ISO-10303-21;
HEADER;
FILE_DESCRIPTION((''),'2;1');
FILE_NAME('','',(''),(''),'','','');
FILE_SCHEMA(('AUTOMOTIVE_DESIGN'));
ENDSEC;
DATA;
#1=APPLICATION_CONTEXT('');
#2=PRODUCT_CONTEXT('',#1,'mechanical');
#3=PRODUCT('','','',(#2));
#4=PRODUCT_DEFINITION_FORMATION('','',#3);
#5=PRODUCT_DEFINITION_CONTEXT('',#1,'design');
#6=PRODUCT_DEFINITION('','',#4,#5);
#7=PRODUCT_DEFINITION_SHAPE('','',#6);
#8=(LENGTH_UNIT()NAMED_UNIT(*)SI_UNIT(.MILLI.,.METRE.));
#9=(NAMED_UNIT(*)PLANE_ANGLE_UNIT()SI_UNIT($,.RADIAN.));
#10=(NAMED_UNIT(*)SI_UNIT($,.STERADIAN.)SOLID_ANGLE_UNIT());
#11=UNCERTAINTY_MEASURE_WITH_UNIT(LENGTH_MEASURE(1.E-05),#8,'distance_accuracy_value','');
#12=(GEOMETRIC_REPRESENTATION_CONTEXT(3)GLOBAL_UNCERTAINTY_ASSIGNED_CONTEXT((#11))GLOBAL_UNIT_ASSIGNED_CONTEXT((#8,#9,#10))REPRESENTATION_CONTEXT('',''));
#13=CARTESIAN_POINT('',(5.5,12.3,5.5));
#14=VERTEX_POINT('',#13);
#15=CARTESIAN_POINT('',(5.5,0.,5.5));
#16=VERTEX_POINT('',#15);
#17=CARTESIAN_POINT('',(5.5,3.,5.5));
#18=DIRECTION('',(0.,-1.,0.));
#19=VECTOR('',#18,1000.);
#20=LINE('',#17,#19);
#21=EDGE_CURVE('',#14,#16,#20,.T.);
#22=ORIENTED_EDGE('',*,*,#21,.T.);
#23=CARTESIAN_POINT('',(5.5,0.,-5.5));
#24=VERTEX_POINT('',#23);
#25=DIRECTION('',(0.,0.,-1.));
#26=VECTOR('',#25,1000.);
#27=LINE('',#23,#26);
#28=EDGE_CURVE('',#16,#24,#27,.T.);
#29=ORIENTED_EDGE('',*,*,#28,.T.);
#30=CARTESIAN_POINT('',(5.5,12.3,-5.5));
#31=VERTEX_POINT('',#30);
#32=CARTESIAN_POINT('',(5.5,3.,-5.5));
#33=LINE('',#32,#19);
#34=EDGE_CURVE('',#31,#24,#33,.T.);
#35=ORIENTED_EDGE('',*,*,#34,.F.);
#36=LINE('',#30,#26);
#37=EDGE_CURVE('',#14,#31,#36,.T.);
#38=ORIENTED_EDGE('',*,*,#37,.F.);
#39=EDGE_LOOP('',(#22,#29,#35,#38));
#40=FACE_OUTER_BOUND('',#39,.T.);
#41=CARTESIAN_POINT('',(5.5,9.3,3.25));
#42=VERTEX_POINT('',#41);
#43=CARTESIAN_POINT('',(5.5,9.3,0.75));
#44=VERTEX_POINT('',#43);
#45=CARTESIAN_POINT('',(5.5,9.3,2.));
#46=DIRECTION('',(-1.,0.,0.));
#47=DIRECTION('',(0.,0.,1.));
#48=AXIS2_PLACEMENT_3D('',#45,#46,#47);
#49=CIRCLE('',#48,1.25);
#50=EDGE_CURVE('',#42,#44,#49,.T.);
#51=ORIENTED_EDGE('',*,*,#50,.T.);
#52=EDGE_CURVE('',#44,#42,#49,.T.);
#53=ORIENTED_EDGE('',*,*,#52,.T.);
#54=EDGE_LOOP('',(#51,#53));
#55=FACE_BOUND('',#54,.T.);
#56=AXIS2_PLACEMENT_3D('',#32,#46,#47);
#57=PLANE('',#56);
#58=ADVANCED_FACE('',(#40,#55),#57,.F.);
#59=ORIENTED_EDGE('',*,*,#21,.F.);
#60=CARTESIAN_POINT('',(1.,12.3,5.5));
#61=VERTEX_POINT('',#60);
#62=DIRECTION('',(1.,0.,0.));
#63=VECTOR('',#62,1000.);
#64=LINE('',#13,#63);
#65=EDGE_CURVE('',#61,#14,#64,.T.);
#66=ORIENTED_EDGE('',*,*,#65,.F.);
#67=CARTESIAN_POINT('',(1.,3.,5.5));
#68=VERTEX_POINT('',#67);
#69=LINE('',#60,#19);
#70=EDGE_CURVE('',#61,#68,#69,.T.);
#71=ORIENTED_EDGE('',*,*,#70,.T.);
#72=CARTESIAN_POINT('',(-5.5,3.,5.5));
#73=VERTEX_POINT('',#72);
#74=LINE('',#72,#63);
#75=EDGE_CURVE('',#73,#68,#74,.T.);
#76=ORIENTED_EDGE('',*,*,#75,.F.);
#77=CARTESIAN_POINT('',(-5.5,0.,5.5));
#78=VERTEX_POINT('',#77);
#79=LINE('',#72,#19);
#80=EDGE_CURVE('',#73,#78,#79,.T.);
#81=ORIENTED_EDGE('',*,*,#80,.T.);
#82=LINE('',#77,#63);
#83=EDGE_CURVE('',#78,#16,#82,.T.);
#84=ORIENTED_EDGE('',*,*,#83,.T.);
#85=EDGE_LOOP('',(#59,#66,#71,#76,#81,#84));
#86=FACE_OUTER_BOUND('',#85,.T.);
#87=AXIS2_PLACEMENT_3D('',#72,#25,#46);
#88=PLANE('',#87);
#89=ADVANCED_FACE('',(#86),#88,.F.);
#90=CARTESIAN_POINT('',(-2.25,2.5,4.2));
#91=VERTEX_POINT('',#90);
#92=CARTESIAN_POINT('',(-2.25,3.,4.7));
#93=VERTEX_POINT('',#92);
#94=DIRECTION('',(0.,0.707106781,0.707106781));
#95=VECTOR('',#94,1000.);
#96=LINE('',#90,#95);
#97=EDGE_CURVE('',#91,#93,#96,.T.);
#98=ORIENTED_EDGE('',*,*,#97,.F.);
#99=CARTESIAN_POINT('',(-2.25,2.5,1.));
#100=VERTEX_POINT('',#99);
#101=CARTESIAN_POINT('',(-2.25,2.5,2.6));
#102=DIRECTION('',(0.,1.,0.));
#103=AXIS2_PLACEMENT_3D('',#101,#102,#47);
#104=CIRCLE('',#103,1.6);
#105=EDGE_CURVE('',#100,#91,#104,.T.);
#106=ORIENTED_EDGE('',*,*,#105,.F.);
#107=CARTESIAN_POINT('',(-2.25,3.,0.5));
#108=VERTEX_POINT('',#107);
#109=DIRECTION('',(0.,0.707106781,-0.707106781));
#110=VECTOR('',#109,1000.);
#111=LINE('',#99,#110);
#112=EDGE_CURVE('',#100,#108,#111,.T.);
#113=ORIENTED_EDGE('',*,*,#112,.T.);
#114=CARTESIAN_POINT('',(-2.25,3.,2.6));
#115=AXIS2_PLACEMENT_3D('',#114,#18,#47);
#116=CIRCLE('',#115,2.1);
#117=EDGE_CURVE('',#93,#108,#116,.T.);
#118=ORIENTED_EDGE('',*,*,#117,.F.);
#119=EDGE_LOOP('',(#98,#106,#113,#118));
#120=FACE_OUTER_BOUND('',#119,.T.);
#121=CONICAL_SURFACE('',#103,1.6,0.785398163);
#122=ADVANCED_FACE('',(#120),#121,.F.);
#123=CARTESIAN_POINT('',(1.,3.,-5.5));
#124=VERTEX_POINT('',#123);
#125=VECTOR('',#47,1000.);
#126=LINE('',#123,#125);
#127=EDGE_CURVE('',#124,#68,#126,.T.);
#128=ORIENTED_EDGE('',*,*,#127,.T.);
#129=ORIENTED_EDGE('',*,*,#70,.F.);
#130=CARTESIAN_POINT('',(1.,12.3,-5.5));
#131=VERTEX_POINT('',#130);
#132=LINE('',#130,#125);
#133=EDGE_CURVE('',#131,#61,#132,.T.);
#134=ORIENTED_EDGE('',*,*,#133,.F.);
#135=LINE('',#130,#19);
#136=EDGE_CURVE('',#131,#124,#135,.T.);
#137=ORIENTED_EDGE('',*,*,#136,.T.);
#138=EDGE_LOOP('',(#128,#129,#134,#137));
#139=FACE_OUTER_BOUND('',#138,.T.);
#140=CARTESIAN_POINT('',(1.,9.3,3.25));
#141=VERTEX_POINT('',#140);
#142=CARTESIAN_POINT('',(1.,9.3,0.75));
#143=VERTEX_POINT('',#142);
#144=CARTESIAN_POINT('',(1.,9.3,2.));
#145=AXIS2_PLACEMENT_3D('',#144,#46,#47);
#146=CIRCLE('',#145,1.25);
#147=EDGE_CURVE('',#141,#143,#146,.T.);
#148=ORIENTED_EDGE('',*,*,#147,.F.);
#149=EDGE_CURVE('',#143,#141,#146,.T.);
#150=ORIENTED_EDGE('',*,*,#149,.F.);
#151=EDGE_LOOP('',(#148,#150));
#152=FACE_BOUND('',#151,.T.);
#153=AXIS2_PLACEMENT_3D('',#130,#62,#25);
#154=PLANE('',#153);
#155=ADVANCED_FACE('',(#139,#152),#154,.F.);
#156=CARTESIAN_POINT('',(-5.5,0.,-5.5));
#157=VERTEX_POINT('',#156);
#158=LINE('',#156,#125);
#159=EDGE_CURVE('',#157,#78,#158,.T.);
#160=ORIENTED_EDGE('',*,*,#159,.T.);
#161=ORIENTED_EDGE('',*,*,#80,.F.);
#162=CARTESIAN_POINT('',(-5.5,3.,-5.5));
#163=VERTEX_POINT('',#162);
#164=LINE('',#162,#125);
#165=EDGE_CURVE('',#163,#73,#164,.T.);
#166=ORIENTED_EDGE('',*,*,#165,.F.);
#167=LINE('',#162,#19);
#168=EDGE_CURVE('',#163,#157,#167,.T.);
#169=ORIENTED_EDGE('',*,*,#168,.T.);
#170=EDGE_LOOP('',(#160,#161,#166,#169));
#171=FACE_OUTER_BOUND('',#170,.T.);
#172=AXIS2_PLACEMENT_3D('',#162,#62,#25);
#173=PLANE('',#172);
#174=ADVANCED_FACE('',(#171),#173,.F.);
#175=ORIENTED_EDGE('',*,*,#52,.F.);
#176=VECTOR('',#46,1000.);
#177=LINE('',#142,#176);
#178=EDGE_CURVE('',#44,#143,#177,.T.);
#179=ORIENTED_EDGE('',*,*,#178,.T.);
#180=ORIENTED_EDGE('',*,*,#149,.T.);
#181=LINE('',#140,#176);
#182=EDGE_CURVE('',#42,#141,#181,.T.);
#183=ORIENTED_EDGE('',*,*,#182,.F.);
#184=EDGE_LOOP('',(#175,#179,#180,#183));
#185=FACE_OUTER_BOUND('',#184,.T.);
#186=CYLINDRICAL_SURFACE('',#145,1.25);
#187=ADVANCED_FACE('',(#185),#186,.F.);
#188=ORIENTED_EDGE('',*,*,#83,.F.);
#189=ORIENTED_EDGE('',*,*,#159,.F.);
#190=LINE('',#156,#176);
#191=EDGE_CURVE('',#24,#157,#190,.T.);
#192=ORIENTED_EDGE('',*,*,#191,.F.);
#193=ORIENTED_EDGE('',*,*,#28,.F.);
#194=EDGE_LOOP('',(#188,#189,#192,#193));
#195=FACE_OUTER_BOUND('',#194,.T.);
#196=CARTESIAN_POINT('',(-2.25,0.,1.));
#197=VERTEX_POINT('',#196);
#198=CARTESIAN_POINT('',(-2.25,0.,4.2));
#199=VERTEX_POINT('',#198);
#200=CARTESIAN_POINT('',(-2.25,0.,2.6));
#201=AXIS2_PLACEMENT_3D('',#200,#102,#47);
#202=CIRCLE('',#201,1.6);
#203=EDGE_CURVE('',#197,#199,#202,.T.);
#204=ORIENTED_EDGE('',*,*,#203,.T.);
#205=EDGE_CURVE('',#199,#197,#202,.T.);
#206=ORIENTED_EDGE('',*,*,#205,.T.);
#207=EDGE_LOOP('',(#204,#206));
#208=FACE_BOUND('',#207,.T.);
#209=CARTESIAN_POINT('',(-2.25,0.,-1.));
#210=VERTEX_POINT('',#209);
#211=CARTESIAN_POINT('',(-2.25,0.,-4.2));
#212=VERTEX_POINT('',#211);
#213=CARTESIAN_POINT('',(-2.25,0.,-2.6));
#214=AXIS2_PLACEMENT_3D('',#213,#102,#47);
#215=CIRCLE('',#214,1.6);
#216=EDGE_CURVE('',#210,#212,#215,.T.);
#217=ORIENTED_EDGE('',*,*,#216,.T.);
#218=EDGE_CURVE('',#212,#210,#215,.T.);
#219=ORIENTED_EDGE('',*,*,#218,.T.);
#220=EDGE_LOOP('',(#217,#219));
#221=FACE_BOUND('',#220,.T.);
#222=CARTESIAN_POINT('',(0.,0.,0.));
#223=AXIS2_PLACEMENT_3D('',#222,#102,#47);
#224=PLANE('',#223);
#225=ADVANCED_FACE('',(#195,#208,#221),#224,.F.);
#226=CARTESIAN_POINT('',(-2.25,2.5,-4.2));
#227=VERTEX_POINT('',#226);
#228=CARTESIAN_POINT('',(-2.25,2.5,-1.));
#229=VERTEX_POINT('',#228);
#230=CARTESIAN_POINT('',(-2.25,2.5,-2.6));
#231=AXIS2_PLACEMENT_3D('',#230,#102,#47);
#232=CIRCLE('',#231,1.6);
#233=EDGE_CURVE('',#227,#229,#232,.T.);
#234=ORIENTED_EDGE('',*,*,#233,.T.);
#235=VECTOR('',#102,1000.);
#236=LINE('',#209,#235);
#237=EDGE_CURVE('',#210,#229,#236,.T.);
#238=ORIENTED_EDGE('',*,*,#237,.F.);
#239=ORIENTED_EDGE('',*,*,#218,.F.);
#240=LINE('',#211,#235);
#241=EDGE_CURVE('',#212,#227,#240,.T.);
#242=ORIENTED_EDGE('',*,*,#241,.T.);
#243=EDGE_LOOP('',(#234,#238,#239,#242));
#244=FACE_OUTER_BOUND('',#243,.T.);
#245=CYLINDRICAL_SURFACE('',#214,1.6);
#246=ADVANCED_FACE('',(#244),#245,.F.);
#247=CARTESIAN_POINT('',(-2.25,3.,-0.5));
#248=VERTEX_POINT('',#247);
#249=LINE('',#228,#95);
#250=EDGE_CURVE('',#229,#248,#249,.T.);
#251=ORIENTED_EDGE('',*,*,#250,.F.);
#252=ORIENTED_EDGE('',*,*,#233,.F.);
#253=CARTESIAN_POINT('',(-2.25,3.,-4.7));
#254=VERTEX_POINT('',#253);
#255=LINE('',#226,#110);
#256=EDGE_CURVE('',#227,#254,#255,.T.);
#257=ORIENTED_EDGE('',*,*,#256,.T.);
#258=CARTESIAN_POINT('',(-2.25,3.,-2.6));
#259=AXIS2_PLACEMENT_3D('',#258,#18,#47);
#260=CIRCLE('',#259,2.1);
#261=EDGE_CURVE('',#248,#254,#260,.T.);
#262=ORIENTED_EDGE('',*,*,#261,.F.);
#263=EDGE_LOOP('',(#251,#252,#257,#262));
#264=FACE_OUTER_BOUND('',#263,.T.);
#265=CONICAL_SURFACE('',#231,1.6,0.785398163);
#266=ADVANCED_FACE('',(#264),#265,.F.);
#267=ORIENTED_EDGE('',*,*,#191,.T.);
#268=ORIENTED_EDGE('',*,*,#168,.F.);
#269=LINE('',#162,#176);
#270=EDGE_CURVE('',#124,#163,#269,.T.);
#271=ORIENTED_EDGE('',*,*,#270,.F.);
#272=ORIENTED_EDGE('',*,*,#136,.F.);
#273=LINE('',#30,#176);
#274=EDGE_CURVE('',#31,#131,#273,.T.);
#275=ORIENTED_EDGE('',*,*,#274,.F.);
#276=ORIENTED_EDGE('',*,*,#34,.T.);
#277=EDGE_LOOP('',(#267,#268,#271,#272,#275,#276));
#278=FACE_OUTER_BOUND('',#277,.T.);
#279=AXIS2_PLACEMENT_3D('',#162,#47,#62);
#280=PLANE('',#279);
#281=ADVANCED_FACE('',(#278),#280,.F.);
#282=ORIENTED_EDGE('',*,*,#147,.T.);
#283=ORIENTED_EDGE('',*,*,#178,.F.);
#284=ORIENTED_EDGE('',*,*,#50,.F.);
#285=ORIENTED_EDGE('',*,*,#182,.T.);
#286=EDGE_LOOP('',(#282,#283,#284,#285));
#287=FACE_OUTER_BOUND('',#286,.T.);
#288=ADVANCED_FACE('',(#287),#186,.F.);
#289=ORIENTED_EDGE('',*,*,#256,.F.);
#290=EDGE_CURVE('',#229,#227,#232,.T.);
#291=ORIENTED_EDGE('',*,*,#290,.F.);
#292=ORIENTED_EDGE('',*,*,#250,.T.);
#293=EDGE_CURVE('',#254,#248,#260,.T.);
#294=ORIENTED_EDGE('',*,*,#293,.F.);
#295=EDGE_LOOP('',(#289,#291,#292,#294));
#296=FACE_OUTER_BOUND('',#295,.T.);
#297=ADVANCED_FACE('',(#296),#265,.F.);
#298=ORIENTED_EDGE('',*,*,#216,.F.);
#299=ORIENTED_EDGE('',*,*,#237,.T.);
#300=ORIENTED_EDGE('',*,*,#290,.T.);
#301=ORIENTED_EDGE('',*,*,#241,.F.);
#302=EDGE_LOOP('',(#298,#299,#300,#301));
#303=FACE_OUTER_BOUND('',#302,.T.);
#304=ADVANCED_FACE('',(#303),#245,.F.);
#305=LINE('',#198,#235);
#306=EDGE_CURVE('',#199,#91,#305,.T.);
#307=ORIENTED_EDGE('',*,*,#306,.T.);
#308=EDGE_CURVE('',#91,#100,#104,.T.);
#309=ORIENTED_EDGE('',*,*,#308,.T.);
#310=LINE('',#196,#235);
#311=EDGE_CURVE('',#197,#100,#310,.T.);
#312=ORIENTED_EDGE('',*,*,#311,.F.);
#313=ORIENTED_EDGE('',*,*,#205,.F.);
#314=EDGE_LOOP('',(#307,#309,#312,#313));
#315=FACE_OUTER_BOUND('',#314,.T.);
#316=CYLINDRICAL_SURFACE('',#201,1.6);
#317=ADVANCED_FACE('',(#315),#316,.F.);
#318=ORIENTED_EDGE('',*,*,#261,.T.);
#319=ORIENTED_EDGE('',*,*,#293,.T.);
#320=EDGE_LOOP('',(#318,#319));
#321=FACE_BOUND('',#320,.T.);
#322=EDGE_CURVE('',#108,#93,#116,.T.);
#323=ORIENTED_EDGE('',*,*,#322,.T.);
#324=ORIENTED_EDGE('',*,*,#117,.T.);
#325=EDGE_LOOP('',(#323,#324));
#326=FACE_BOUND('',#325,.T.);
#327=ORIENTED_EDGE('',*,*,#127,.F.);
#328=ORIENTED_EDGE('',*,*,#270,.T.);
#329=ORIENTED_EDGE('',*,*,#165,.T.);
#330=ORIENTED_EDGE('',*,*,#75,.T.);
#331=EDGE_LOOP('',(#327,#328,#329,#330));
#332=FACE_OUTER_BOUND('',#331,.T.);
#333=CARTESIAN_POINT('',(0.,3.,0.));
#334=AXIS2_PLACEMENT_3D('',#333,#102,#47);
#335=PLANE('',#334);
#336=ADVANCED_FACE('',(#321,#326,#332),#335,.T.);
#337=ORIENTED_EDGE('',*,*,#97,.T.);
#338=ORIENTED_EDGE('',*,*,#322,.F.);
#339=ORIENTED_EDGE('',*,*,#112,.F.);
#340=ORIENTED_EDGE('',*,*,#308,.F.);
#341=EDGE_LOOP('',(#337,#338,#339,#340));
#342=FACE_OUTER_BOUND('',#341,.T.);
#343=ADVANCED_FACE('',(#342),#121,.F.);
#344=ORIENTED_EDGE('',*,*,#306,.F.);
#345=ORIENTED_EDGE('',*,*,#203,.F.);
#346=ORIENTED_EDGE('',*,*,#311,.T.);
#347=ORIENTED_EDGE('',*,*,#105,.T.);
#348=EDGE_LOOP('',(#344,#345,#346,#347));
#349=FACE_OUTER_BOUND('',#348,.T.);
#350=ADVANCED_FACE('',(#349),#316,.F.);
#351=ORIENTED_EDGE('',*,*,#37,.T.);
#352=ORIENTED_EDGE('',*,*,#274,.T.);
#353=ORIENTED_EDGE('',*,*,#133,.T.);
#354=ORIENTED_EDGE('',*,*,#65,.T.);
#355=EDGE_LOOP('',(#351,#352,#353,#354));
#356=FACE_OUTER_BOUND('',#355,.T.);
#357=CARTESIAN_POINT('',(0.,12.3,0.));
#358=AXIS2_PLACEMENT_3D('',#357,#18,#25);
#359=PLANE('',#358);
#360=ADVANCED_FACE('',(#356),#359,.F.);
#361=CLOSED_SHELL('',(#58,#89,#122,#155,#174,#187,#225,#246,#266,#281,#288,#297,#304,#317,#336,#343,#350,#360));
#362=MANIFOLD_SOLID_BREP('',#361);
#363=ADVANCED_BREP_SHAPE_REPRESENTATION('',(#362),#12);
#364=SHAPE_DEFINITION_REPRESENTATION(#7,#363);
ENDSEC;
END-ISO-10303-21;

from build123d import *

# Parameters (mm, degrees)
SKETCH1_W             = 11
SKETCH1_H             = 11
BOSS_EXTRUDE1_DEPTH   = 3
SKETCH2_W             = 4.5
SKETCH2_H             = 11
BOSS_EXTRUDE2_DEPTH   = 9.3
M3_TAPPED_HOLE1_D     = 2.5
M3_TAPPED_HOLE1_DEPTH = 8.5
M3_TAPPED_HOLE1_TIP   = 0.751075774
SKETCH5_R             = 1.6
CUT_EXTRUDE1_DEPTH    = 13.123943253
CHAMFER1_SIZE         = 0.5


with BuildPart() as part:
    # Sketch1 → Boss-Extrude1 (new body)
    with BuildSketch(Plane(origin=(0, 0, 0), x_dir=(1, 0, 0), z_dir=(0, 1, 0))):
        Rectangle(SKETCH1_W, SKETCH1_H)
    extrude(amount=BOSS_EXTRUDE1_DEPTH)

    # Sketch2 → Boss-Extrude2 (add)
    with BuildSketch(Plane(origin=(0, 3, 0), x_dir=(1, 0, 0), z_dir=(0, 1, 0))):
        with Locations((3.25, 0)):
            Rectangle(SKETCH2_W, SKETCH2_H)
    extrude(amount=BOSS_EXTRUDE2_DEPTH)

    # M3 Tapped Hole1
    with Locations(Plane.ZY.offset(-1)):
        with Locations((2, 9.3)):
            Hole(M3_TAPPED_HOLE1_D / 2, depth=M3_TAPPED_HOLE1_DEPTH)
            with Locations((0, 0, -(M3_TAPPED_HOLE1_DEPTH + M3_TAPPED_HOLE1_TIP / 2))):  # 118° drill point
                Cone(0, M3_TAPPED_HOLE1_D / 2, M3_TAPPED_HOLE1_TIP, mode=Mode.SUBTRACT)

    # Sketch5 → Cut-Extrude1 (cut, through all)
    with BuildSketch(Plane(origin=(0, 3, 0), x_dir=(1, 0, 0), z_dir=(0, 1, 0))):
        with Locations(Location((-2.25, 2.6, 0), (0, 0, 270))):
            Circle(SKETCH5_R)
        with Locations(Location((-2.25, -2.6, 0), (0, 0, 270))):
            Circle(SKETCH5_R)
    extrude(amount=-CUT_EXTRUDE1_DEPTH, mode=Mode.SUBTRACT)

    # Chamfer1
    chamfer1_edges = [part.edges().sort_by_distance(p)[0] for p in [
        (-2.25, 3, -4.2),
        (-2.25, 3, 1),
    ]]
    chamfer(chamfer1_edges, length=CHAMFER1_SIZE)


solid = part.part
